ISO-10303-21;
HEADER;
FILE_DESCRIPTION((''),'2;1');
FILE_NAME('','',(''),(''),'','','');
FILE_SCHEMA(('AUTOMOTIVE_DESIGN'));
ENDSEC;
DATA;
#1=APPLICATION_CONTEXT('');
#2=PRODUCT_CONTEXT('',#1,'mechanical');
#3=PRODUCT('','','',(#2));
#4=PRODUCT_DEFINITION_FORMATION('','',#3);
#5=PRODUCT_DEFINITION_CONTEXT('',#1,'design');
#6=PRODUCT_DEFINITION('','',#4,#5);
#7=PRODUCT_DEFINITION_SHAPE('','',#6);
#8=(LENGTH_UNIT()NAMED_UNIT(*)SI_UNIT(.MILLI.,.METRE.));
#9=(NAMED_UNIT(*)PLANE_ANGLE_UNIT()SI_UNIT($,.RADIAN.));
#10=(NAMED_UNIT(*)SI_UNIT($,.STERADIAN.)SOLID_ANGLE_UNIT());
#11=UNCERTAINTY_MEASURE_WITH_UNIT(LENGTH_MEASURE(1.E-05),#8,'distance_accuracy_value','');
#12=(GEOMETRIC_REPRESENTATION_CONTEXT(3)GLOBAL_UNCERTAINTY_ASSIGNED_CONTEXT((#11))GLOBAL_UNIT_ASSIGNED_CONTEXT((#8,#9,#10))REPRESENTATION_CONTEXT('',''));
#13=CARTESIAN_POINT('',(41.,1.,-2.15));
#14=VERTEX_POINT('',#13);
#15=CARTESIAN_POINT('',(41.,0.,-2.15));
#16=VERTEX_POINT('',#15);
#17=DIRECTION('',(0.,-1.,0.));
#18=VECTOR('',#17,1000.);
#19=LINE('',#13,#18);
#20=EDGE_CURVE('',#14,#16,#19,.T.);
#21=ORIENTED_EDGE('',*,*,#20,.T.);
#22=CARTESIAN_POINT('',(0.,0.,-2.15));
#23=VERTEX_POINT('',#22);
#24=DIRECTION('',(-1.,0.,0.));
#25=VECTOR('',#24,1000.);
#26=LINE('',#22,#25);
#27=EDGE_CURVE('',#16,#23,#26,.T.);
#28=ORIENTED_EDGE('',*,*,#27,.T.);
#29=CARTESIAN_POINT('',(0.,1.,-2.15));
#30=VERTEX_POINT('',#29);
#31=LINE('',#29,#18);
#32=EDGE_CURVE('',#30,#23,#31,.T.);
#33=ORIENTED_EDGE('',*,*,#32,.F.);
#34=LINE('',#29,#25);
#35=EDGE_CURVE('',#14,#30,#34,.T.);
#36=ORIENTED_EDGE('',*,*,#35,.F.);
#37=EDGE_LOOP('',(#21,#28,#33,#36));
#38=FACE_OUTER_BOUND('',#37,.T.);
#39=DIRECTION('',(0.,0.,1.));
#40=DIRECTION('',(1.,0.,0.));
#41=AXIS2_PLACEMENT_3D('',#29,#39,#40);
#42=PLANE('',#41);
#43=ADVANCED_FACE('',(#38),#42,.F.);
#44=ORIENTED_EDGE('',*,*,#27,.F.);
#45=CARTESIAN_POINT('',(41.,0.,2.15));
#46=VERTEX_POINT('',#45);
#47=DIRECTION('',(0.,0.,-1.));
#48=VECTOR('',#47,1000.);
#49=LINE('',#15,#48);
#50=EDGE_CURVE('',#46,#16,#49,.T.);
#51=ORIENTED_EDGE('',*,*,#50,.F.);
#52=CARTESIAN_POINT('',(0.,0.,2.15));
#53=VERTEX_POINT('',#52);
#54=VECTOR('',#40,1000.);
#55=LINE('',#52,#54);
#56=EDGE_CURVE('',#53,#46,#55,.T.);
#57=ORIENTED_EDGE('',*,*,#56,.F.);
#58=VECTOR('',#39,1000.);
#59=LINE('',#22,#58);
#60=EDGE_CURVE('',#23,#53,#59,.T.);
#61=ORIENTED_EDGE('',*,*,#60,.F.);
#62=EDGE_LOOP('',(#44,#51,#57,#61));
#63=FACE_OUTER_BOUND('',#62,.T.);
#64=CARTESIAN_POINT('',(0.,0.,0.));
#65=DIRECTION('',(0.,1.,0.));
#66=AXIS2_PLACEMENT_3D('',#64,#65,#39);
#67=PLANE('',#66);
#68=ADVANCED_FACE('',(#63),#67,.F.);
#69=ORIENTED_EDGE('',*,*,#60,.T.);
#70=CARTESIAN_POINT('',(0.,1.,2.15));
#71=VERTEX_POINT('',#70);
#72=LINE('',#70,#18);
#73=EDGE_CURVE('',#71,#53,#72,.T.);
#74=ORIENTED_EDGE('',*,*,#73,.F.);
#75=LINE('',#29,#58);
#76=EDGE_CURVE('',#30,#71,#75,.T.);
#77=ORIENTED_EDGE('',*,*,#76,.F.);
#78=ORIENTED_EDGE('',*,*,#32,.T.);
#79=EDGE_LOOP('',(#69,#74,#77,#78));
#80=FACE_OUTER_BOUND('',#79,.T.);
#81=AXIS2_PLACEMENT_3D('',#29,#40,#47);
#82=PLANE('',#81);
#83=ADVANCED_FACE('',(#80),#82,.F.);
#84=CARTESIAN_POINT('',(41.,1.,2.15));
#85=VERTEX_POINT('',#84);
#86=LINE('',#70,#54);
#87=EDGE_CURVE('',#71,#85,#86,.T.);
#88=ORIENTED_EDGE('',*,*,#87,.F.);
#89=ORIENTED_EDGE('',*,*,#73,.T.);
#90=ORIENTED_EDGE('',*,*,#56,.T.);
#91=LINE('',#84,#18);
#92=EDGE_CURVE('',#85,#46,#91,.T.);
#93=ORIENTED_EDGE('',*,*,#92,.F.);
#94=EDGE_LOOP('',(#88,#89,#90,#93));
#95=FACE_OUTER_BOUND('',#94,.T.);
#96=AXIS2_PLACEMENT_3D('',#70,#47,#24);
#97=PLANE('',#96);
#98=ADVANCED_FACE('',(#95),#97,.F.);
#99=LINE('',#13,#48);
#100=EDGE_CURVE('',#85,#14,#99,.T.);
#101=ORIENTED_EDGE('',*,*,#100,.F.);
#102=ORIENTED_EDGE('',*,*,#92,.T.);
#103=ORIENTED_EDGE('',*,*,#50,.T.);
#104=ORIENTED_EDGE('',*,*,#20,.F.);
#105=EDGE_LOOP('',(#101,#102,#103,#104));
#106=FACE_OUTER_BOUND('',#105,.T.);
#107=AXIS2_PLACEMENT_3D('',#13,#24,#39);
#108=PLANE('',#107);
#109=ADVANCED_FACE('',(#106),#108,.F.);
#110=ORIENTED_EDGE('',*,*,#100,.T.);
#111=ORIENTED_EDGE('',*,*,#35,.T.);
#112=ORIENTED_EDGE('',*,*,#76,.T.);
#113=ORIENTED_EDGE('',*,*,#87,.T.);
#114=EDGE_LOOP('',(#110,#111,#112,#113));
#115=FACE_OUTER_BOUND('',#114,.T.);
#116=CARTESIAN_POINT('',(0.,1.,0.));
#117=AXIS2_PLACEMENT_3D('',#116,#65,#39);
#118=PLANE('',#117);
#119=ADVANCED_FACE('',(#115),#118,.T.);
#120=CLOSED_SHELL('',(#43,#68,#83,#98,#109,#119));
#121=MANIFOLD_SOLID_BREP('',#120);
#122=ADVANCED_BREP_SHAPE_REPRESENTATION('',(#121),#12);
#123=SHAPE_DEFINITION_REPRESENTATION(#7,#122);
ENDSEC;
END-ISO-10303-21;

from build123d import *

# Parameters (mm, degrees)
SKETCH1_W           = 41
SKETCH1_H           = 4.3
BOSS_EXTRUDE1_DEPTH = 1


with BuildPart() as part:
    # Sketch1 → Boss-Extrude1 (new body)
    with BuildSketch(Plane(origin=(0, 0, 0), x_dir=(1, 0, 0), z_dir=(0, 1, 0))):
        with Locations((20.5, 0)):
            Rectangle(SKETCH1_W, SKETCH1_H)
    extrude(amount=BOSS_EXTRUDE1_DEPTH)


solid = part.part
